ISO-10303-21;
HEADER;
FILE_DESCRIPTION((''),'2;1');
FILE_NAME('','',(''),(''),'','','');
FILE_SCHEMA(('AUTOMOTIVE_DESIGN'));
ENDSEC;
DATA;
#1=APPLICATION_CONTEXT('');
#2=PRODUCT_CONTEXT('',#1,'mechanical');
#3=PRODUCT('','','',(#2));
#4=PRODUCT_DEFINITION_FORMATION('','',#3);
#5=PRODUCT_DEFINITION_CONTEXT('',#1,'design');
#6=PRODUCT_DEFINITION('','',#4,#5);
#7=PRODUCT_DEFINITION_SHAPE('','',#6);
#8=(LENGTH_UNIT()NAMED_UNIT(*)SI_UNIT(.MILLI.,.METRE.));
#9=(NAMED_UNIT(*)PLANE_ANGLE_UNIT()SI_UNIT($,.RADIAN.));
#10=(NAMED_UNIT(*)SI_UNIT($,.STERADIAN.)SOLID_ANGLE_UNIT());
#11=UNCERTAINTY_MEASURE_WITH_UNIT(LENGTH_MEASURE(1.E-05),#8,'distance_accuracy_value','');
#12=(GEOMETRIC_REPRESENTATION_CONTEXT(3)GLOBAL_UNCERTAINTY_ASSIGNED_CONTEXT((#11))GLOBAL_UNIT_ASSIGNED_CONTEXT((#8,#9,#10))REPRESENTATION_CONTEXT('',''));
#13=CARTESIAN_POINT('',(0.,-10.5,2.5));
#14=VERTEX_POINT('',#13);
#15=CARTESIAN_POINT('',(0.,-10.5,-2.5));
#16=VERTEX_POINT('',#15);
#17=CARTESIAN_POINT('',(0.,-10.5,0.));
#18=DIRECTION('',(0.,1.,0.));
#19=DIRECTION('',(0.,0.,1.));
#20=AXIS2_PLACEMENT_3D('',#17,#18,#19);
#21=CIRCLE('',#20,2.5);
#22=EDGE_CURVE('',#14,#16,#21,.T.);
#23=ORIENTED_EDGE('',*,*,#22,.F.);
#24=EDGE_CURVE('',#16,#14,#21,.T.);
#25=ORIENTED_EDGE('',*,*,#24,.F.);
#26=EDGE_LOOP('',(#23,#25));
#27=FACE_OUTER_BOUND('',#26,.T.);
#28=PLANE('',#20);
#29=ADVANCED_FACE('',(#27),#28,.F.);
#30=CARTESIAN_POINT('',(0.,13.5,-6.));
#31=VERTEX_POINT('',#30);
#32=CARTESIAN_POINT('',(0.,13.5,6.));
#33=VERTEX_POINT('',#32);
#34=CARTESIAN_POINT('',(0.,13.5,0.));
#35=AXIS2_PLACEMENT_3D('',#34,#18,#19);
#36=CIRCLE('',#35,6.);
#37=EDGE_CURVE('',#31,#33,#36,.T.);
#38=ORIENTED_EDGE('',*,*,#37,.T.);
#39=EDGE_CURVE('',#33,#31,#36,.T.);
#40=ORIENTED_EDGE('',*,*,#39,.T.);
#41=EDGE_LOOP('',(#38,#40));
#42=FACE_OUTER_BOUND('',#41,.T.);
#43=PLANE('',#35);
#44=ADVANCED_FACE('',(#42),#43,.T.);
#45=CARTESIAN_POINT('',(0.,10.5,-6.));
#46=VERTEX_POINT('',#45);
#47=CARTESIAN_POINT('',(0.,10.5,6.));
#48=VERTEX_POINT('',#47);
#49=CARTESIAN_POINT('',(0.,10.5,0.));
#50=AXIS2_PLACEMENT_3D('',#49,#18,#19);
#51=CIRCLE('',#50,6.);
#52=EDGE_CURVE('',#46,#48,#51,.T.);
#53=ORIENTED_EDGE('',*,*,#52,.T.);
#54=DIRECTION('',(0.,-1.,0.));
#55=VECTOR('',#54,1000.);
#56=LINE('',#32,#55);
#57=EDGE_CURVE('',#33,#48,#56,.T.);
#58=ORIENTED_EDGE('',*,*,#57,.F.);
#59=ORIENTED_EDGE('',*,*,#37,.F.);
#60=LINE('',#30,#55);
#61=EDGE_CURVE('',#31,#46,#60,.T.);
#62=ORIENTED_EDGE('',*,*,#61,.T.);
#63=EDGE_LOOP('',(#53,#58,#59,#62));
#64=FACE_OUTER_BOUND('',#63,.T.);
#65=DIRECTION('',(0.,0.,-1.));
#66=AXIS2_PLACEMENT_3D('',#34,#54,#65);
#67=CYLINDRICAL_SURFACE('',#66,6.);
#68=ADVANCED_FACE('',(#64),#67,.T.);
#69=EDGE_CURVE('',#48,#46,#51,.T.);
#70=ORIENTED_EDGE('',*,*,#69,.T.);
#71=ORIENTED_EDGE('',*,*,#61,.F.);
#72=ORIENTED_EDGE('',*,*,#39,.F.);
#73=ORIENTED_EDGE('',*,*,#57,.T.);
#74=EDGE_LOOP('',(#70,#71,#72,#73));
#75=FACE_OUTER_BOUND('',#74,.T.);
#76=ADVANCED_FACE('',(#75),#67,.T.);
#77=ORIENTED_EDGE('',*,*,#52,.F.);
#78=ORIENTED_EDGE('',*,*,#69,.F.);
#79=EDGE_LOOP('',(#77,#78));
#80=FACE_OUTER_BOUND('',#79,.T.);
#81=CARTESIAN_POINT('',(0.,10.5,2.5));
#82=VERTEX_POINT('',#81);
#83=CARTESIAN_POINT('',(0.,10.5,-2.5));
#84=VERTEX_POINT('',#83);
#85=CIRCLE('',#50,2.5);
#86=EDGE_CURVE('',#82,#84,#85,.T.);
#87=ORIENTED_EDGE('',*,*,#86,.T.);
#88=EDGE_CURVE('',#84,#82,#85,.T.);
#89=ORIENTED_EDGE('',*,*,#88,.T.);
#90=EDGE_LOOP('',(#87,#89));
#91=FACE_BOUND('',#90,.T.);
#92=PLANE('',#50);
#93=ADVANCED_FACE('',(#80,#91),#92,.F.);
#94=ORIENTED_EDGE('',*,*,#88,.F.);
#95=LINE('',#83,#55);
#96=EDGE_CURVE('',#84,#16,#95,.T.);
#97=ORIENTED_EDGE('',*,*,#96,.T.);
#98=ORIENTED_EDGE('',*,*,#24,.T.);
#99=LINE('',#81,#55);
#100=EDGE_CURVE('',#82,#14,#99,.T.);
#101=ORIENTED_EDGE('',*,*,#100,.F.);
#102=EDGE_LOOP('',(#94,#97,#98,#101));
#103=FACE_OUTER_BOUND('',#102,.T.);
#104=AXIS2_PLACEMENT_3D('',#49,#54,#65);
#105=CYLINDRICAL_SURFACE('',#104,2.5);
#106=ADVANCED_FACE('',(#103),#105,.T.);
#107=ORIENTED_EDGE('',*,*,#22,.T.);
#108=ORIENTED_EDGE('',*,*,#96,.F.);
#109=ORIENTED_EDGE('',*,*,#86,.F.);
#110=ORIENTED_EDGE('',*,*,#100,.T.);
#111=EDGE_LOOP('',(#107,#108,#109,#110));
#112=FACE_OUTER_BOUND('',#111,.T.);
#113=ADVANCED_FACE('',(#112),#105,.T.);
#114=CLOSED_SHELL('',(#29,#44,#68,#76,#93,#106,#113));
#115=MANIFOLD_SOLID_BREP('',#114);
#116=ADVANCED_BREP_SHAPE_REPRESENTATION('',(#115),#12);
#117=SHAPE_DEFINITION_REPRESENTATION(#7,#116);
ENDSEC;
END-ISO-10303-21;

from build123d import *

# Parameters (mm, degrees)
SHANK_PROFILE_5_R = 2.5
SHANK_5X21_DEPTH  = 10.5
HEAD_PROFILE_12_R = 6
HEAD_12X3_DEPTH   = 3


with BuildPart() as part:
    # Shank Profile Ø5 → Shank Ø5x21 (new, symmetric)
    with BuildSketch(Plane(origin=(0, 0, 0), x_dir=(1, 0, 0), z_dir=(0, 1, 0))):
        with Locations(Location((0, 0, 0), (0, 0, 90))):
            Circle(SHANK_PROFILE_5_R)
    extrude(amount=SHANK_5X21_DEPTH, both=True)

    # Head Profile Ø12 → Head Ø12x3 (add)
    with BuildSketch(Plane(origin=(0, 10.5, 0), x_dir=(1, 0, 0), z_dir=(0, 1, 0))):
        with Locations(Location((0, 0, 0), (0, 0, 270))):
            Circle(HEAD_PROFILE_12_R)
    extrude(amount=HEAD_12X3_DEPTH)


solid = part.part
